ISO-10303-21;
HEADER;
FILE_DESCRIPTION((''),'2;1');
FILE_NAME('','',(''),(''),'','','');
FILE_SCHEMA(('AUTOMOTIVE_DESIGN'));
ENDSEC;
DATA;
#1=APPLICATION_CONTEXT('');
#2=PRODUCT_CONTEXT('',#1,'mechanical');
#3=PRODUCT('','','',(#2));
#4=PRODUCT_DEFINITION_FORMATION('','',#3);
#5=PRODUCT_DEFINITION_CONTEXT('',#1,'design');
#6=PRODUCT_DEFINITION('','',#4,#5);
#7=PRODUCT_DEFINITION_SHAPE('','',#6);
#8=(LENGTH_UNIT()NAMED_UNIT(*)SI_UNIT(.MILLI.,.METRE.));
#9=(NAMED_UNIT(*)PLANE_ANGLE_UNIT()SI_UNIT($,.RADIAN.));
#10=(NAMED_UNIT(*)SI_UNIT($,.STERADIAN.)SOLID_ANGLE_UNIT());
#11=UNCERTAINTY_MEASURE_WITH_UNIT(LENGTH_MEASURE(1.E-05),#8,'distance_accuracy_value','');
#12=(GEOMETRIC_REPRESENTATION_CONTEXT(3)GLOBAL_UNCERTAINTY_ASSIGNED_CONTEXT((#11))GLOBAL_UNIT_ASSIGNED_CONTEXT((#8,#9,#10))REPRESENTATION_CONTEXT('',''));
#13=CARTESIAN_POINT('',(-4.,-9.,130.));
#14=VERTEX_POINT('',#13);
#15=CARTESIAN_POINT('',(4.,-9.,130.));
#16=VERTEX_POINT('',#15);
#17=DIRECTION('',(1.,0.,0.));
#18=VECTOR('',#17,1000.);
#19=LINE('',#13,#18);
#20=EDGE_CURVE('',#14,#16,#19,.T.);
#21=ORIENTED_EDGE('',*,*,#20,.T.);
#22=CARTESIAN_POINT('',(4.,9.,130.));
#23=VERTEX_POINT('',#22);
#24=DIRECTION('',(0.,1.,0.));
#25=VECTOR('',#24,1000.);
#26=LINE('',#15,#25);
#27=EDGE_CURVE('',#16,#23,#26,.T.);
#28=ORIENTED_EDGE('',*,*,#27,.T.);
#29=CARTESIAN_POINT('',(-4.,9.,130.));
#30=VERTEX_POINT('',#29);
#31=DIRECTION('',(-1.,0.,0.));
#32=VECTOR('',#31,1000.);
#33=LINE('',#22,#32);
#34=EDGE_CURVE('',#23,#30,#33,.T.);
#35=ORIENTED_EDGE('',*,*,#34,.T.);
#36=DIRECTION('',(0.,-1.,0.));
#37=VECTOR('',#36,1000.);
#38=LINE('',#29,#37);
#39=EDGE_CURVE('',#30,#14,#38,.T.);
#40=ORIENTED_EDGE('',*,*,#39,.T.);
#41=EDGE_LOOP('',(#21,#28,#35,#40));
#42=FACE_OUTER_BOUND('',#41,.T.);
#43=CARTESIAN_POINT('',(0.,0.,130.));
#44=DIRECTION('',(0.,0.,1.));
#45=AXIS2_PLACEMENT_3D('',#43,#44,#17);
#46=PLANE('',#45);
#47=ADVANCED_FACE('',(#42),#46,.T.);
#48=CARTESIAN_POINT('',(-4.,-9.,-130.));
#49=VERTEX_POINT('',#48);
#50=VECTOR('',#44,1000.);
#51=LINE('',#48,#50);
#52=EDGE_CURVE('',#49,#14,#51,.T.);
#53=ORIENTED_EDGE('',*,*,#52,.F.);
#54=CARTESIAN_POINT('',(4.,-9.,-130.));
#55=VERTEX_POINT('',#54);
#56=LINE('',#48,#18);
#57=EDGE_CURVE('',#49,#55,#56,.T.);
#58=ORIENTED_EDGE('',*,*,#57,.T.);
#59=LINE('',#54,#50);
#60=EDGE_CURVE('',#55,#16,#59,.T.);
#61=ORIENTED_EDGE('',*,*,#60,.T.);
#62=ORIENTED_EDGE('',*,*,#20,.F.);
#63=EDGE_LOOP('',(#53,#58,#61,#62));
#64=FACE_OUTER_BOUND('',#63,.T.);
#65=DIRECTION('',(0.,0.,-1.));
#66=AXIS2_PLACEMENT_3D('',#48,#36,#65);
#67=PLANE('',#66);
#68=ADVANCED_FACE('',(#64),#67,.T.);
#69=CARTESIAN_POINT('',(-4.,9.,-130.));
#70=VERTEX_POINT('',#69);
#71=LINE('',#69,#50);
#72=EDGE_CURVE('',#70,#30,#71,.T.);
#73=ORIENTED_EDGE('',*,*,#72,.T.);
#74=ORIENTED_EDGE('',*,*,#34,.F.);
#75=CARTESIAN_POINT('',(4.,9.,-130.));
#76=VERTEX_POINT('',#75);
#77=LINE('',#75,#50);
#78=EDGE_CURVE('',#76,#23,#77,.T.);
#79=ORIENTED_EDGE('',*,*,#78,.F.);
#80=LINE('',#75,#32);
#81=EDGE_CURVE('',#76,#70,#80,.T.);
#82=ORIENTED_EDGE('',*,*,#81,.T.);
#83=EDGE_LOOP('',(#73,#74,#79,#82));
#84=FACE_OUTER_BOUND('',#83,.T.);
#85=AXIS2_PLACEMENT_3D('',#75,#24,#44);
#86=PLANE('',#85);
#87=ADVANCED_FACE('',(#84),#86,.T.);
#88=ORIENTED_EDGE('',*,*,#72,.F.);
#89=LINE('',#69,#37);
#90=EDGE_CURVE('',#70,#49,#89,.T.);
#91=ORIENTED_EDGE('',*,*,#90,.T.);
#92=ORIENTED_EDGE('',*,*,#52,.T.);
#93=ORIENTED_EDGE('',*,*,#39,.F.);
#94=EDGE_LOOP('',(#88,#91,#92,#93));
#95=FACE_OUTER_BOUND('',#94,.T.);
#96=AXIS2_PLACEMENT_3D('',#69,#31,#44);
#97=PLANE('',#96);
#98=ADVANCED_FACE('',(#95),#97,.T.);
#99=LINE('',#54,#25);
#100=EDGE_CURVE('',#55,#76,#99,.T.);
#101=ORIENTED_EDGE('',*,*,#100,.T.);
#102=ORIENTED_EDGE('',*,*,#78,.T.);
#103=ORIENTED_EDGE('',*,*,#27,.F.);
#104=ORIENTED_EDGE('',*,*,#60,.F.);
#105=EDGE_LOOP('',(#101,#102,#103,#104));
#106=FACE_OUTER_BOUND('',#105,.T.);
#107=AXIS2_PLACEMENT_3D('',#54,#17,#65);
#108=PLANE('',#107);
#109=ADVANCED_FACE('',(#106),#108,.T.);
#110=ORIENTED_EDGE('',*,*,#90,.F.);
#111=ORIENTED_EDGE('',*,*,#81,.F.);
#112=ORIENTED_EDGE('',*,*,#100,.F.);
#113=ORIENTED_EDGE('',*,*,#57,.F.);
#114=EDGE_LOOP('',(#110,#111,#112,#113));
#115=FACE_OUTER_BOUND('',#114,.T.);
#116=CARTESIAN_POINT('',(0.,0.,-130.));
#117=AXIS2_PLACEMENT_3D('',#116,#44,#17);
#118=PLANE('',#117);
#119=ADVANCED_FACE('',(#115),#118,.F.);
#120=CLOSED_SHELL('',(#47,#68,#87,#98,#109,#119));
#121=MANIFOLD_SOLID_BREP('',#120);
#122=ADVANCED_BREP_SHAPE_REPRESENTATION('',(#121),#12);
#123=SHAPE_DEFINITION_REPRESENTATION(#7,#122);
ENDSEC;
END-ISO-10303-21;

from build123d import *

# Parameters (mm, degrees)
SKETCH_1_W      = 8
SKETCH_1_H      = 18
EXTRUDE_1_DEPTH = 130


with BuildPart() as part:
    # 草图1 → 凸台-拉伸1 (new, symmetric)
    with BuildSketch(Plane.XY):
        Rectangle(SKETCH_1_W, SKETCH_1_H)
    extrude(amount=EXTRUDE_1_DEPTH, both=True)


solid = part.part
